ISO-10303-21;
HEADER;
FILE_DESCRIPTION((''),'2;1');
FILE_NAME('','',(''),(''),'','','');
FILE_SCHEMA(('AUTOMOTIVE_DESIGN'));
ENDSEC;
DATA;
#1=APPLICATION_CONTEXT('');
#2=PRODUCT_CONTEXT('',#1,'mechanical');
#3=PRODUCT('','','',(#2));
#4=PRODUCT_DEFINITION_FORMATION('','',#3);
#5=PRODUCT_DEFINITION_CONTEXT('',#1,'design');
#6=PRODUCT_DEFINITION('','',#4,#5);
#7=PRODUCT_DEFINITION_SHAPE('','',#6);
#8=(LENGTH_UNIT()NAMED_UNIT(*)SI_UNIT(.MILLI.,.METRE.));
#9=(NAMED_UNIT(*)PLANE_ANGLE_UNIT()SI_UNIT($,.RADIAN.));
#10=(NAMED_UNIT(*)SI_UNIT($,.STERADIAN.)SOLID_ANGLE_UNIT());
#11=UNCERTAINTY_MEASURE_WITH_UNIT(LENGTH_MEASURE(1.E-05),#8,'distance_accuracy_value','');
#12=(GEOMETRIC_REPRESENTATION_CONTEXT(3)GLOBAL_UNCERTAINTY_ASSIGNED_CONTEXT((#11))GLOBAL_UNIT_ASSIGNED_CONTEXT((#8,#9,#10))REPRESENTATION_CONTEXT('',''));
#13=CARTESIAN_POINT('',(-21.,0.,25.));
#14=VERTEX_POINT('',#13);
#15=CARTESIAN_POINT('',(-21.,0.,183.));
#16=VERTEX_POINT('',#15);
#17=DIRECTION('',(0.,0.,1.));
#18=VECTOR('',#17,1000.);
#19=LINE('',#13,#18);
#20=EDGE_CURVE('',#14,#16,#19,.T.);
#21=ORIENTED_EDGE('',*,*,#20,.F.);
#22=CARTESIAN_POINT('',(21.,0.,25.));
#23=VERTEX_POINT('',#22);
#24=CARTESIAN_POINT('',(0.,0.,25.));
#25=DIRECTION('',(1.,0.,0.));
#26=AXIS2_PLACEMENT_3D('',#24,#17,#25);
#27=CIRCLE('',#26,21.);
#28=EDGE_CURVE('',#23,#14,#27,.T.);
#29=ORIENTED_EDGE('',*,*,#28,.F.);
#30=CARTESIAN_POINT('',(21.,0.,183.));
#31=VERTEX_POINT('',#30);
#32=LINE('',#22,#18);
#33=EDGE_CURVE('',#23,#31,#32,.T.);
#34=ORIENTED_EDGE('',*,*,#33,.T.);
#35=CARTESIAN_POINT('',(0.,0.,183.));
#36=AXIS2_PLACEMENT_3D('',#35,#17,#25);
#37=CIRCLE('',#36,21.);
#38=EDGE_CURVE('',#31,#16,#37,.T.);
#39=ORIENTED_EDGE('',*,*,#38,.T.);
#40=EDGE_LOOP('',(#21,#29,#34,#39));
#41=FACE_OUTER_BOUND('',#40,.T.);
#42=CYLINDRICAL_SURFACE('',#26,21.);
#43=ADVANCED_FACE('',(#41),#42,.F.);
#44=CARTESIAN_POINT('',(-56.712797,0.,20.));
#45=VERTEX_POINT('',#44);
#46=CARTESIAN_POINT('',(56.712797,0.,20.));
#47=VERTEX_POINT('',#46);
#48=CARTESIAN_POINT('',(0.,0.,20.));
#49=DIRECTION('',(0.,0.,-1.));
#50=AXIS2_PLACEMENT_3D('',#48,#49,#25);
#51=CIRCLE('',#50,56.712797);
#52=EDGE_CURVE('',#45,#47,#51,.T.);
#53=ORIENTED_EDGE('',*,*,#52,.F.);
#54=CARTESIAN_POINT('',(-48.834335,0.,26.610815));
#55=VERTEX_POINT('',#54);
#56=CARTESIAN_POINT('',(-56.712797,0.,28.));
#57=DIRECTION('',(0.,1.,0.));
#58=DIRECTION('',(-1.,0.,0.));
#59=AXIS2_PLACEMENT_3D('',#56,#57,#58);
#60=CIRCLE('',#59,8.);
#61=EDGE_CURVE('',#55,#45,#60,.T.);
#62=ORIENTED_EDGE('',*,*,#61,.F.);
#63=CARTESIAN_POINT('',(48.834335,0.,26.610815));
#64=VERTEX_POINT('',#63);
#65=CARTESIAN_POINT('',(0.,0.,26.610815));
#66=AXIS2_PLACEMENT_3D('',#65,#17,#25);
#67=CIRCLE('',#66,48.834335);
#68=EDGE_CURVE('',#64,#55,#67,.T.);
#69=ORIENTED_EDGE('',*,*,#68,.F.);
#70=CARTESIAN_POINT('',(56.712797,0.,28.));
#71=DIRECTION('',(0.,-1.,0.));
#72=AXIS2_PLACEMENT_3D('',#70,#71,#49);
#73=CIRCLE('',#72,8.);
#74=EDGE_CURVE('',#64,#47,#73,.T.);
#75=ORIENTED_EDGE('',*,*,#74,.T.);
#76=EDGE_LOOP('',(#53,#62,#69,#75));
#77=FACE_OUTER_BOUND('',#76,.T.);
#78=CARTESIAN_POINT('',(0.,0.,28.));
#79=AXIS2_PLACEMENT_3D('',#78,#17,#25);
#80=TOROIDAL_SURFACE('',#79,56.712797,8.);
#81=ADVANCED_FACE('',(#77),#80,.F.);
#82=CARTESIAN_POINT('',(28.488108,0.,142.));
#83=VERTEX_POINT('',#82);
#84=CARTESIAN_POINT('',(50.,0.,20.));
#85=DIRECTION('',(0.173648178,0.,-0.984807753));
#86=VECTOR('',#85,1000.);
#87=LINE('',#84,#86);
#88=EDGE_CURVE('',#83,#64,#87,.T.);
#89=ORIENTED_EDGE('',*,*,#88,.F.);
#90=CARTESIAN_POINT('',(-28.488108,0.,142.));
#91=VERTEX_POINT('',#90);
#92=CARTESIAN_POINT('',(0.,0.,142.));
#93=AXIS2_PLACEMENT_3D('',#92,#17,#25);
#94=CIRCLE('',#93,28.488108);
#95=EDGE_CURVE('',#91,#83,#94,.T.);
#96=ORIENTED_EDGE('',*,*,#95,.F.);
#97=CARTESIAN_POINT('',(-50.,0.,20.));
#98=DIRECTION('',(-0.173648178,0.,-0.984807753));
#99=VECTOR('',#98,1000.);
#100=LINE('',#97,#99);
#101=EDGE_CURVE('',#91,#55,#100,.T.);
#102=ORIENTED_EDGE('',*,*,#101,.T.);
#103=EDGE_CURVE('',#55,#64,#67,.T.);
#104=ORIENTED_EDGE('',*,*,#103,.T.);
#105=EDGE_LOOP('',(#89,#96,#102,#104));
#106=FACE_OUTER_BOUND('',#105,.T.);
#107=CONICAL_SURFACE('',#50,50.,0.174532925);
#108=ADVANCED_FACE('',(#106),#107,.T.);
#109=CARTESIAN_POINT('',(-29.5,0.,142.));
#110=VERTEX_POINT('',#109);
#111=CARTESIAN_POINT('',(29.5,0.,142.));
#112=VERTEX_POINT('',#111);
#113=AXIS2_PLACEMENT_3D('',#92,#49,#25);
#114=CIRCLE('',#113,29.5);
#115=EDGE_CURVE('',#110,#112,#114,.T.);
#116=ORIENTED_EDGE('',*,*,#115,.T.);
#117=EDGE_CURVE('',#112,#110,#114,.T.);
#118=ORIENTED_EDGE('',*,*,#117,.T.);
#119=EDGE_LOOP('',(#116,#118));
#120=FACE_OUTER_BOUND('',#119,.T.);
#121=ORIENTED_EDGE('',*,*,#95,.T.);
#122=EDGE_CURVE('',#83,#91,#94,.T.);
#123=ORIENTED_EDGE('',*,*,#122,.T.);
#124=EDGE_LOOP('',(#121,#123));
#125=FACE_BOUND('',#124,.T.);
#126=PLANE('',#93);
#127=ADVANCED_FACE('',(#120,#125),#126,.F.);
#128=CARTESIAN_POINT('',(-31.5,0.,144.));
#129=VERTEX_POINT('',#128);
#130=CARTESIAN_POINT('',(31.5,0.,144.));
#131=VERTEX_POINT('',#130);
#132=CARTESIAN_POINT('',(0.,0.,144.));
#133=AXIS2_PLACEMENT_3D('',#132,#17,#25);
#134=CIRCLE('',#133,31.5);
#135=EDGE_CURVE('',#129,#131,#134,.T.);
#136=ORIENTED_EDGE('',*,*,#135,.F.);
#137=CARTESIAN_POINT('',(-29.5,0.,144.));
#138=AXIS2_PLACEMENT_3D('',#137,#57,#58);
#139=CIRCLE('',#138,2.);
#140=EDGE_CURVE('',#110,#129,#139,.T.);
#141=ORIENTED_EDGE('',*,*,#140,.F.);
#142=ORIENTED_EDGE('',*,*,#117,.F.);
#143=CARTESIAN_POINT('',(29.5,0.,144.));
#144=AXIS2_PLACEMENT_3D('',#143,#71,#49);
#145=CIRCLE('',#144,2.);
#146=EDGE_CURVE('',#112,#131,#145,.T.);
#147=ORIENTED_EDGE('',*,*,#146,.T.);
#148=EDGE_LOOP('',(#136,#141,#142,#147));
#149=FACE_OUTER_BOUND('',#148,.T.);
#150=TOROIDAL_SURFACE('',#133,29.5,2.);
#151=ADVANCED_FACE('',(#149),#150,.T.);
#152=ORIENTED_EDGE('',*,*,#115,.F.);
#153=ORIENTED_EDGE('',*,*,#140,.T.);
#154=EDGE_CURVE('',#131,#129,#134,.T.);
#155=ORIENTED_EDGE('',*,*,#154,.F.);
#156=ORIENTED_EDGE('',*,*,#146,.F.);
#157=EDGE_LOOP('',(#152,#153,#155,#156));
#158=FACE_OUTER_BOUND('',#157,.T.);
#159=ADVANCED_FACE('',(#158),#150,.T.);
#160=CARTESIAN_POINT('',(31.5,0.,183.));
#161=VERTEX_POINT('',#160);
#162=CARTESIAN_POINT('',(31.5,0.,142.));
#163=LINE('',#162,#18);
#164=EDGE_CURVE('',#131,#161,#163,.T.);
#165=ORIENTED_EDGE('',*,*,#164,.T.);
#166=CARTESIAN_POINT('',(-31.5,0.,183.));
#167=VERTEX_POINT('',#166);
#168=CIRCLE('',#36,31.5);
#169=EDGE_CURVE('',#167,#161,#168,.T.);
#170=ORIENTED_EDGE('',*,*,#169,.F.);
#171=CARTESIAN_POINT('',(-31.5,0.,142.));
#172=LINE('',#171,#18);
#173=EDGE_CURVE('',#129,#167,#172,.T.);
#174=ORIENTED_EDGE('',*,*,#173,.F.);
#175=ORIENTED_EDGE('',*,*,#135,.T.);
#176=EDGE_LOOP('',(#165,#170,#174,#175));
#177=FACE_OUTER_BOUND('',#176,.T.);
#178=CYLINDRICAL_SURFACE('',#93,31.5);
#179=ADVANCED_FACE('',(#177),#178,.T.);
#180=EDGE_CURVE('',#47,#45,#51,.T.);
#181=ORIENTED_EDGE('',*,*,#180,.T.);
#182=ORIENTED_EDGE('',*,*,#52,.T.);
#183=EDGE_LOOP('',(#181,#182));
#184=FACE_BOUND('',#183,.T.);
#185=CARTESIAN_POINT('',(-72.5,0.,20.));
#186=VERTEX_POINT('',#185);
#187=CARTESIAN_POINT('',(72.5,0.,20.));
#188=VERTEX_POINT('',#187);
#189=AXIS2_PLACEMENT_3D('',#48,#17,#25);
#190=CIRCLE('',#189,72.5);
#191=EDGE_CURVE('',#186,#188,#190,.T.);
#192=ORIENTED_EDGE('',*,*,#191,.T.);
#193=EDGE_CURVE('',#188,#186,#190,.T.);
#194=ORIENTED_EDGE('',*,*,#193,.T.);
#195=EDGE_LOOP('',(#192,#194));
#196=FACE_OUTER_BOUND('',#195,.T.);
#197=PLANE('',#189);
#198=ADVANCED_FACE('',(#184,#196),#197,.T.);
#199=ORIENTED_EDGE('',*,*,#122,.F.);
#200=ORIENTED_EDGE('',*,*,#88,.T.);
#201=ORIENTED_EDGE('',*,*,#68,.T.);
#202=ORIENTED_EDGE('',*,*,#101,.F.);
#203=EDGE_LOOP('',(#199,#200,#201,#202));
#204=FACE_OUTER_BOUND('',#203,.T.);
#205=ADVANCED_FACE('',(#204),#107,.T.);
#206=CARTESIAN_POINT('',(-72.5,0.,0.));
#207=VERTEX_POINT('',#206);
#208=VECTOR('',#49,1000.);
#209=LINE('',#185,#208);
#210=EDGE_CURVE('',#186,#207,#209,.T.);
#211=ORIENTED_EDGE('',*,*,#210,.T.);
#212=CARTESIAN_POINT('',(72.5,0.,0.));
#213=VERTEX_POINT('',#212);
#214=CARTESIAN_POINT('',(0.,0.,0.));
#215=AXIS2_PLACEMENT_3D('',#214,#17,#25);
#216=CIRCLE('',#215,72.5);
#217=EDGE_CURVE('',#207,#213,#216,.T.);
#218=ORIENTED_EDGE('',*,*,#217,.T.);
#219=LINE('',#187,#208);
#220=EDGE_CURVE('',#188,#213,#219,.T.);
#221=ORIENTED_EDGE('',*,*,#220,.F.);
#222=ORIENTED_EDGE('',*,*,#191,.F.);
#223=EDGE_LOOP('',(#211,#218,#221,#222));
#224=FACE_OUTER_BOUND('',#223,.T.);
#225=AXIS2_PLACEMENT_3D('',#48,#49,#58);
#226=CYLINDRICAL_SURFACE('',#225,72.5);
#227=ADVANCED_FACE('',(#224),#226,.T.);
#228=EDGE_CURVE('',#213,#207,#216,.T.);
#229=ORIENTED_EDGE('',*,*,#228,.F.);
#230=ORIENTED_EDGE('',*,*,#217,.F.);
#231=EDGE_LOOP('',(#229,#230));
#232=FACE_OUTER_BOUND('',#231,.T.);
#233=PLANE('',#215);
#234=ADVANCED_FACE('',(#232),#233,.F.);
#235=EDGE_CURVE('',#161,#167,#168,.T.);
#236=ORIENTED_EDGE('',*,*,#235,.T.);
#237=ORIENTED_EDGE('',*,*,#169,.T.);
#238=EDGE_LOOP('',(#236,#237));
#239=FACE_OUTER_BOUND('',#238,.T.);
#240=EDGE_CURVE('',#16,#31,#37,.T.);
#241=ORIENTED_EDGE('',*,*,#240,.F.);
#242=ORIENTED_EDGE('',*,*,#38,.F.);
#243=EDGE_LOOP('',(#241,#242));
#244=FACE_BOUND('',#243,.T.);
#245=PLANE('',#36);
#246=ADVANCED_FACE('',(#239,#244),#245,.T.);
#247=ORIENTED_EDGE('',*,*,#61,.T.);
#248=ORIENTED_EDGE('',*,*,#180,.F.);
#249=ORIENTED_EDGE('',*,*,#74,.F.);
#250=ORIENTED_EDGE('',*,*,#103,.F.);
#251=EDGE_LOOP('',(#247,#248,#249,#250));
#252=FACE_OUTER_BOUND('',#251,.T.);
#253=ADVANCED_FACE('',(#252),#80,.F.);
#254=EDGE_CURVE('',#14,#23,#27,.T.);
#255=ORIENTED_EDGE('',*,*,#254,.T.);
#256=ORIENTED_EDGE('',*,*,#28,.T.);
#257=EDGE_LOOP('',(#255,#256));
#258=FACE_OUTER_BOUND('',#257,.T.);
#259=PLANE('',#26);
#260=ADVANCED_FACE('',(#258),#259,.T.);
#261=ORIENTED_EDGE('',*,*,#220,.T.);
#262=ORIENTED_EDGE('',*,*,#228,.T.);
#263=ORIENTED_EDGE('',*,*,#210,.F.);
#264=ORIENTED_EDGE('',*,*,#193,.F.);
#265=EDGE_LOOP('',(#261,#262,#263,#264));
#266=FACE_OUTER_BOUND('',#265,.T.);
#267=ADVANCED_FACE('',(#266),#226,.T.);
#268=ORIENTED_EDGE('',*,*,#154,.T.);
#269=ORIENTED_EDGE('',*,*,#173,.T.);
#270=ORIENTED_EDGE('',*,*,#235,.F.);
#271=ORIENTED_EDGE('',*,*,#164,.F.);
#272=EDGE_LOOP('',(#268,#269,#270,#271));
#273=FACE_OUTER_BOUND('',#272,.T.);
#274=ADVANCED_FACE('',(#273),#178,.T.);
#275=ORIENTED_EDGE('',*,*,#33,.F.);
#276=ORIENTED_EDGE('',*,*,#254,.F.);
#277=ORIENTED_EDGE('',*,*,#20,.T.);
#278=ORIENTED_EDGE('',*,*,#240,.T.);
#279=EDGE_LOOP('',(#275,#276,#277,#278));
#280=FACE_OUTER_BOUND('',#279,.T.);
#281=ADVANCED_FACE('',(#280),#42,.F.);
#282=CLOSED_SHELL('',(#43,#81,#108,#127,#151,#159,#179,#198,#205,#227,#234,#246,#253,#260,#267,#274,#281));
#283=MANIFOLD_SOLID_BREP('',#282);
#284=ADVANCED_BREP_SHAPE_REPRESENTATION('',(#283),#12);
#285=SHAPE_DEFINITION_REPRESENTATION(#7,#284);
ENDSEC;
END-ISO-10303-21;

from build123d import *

# Parameters (mm, degrees)
FLANGE_SKETCH_145_R                = 72.5
FLANGE_145X20_DEPTH                = 20
TAPER_SKETCH_100_R                 = 50
TAPERED_BODY_100_10DEG_DRAFT_DEPTH = 125
TAPERED_BODY_100_10DEG_DRAFT_TAPER = 10
SPIGOT_63X38_DEPTH                 = 38
SPIGOT_63X38_DEPTH_BACK            = 3
SPIGOT_SKETCH_63_R                 = 31.5
BORE_SKETCH_42_R                   = 21
BORE_42X158_DEPTH                  = 158
FLANGE_ROOT_FILLET_R8_R            = 8
SPIGOT_EDGE_FILLET_R2_R            = 2


with BuildPart() as part:
    # Flange Sketch Ø145 → Flange Ø145x20 (new body)
    with BuildSketch(Plane.XY):
        Circle(FLANGE_SKETCH_145_R)
    extrude(amount=FLANGE_145X20_DEPTH)

    # Taper Sketch Ø100 → Tapered Body Ø100 10deg Draft (add)
    with BuildSketch(Plane.XY.offset(20)):
        Circle(TAPER_SKETCH_100_R)
    extrude(amount=TAPERED_BODY_100_10DEG_DRAFT_DEPTH, taper=TAPERED_BODY_100_10DEG_DRAFT_TAPER)

    # Spigot Sketch Ø63 → Spigot Ø63x38 (add, two sides: drawn at the far end of the back side and taken through both)
    with BuildSketch(Plane.XY.offset(145).offset(-SPIGOT_63X38_DEPTH_BACK)):
        Circle(SPIGOT_SKETCH_63_R)
    extrude(amount=SPIGOT_63X38_DEPTH + SPIGOT_63X38_DEPTH_BACK)

    # Bore Sketch Ø42 → Bore Ø42x158 (cut)
    with BuildSketch(Plane.XY.offset(183)):
        Circle(BORE_SKETCH_42_R)
    extrude(amount=-BORE_42X158_DEPTH, mode=Mode.SUBTRACT)

    # Flange Root Fillet R8
    flange_root_fillet_r8_edges = [part.edges().sort_by_distance(p)[0] for p in [
        (-50, 0, 20),
    ]]
    fillet(flange_root_fillet_r8_edges, radius=FLANGE_ROOT_FILLET_R8_R)

    # Spigot Edge Fillet R2
    spigot_edge_fillet_r2_edges = [part.edges().sort_by_distance(p)[0] for p in [
        (-31.5, 0, 142),
    ]]
    fillet(spigot_edge_fillet_r2_edges, radius=SPIGOT_EDGE_FILLET_R2_R)


solid = part.part
